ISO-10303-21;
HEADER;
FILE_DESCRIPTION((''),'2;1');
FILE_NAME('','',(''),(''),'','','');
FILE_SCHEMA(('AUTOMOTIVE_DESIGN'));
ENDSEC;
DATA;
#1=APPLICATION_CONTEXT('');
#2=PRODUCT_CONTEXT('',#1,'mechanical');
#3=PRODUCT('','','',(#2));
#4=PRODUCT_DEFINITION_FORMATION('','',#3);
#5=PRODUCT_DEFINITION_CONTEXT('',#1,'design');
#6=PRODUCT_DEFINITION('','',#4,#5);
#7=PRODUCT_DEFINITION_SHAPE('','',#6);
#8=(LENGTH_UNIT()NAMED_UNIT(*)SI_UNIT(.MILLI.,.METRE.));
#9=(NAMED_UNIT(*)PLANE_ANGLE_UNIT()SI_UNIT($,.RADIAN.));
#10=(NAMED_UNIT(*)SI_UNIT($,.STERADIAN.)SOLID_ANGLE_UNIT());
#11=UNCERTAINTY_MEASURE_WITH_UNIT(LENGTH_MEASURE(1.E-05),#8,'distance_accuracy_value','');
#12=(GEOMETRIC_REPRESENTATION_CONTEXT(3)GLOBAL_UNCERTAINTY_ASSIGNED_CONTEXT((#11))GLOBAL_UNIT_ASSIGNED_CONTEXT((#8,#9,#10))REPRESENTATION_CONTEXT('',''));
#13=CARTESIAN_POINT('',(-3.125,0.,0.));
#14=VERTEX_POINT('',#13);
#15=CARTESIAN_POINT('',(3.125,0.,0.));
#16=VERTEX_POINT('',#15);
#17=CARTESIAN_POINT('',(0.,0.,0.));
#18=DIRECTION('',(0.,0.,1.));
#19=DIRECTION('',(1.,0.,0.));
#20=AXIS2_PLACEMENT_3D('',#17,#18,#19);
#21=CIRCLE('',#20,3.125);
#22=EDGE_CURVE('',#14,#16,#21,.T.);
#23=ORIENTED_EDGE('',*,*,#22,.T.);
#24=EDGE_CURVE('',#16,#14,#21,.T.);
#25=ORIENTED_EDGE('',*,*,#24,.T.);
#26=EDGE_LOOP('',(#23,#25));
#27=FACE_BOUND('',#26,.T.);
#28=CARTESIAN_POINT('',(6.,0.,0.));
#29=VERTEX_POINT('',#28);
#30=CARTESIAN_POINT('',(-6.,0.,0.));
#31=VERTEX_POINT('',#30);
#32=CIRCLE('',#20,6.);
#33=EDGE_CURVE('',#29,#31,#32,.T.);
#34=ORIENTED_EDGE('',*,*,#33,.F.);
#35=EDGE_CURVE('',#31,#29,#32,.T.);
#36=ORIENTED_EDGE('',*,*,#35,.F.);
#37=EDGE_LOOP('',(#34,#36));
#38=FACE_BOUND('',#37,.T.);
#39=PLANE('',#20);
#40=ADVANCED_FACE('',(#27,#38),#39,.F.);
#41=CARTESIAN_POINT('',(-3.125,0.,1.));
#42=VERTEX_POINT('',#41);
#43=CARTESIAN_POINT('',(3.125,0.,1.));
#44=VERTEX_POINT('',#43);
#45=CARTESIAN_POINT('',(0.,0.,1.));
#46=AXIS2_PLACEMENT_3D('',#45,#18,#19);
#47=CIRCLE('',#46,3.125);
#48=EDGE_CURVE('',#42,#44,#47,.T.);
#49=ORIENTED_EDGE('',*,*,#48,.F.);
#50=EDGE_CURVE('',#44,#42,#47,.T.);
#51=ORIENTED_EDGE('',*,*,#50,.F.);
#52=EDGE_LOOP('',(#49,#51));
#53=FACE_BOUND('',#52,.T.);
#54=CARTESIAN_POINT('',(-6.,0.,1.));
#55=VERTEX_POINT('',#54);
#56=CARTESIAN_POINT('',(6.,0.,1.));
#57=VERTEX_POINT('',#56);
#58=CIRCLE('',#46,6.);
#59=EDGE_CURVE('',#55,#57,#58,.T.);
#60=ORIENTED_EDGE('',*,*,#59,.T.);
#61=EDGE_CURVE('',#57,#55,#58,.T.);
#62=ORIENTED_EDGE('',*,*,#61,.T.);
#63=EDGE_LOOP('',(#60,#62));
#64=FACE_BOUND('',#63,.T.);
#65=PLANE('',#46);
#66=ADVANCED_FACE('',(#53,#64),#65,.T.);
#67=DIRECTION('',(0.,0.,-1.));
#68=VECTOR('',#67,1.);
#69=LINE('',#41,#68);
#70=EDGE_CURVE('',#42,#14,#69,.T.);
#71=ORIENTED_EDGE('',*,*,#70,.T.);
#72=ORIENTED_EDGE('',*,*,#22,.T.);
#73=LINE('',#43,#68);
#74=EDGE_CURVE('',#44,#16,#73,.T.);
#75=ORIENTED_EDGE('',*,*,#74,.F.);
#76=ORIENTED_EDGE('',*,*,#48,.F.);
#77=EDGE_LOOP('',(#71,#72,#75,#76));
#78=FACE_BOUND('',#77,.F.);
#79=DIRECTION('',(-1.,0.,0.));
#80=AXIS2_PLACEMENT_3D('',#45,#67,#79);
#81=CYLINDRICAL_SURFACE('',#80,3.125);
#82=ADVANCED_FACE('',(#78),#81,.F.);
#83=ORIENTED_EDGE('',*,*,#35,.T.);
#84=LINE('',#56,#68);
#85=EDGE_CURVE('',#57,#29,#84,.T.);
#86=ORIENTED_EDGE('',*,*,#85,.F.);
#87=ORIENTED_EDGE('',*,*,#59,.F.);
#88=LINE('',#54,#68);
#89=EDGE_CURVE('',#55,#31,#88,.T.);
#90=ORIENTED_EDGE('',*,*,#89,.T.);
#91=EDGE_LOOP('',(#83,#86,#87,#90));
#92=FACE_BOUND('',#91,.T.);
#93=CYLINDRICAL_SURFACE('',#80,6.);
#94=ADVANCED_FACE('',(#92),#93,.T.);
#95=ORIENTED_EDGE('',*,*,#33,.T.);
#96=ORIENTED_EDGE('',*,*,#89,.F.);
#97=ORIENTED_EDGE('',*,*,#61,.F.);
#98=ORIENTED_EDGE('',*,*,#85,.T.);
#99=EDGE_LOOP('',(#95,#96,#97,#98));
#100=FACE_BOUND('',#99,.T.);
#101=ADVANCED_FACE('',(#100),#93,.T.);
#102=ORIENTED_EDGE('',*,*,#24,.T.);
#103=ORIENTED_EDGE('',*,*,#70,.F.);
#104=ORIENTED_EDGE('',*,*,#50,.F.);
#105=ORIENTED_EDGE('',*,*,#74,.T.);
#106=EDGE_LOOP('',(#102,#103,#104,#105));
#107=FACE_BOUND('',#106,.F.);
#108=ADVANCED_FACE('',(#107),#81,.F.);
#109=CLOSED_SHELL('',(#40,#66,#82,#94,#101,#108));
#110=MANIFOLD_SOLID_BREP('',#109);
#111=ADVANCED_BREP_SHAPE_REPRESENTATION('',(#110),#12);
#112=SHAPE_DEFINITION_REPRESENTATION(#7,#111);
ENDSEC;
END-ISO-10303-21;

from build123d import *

# Parameters (mm, degrees)
SKETCH2_R           = 6
SKETCH2_R_2         = 3.125
BOSS_EXTRUDE1_DEPTH = 1


with BuildPart() as part:
    # Sketch2 → Boss-Extrude1 (new body)
    with BuildSketch(Plane.XY):
        Circle(SKETCH2_R)
        Circle(SKETCH2_R_2, mode=Mode.SUBTRACT)
    extrude(amount=BOSS_EXTRUDE1_DEPTH)


solid = part.part
